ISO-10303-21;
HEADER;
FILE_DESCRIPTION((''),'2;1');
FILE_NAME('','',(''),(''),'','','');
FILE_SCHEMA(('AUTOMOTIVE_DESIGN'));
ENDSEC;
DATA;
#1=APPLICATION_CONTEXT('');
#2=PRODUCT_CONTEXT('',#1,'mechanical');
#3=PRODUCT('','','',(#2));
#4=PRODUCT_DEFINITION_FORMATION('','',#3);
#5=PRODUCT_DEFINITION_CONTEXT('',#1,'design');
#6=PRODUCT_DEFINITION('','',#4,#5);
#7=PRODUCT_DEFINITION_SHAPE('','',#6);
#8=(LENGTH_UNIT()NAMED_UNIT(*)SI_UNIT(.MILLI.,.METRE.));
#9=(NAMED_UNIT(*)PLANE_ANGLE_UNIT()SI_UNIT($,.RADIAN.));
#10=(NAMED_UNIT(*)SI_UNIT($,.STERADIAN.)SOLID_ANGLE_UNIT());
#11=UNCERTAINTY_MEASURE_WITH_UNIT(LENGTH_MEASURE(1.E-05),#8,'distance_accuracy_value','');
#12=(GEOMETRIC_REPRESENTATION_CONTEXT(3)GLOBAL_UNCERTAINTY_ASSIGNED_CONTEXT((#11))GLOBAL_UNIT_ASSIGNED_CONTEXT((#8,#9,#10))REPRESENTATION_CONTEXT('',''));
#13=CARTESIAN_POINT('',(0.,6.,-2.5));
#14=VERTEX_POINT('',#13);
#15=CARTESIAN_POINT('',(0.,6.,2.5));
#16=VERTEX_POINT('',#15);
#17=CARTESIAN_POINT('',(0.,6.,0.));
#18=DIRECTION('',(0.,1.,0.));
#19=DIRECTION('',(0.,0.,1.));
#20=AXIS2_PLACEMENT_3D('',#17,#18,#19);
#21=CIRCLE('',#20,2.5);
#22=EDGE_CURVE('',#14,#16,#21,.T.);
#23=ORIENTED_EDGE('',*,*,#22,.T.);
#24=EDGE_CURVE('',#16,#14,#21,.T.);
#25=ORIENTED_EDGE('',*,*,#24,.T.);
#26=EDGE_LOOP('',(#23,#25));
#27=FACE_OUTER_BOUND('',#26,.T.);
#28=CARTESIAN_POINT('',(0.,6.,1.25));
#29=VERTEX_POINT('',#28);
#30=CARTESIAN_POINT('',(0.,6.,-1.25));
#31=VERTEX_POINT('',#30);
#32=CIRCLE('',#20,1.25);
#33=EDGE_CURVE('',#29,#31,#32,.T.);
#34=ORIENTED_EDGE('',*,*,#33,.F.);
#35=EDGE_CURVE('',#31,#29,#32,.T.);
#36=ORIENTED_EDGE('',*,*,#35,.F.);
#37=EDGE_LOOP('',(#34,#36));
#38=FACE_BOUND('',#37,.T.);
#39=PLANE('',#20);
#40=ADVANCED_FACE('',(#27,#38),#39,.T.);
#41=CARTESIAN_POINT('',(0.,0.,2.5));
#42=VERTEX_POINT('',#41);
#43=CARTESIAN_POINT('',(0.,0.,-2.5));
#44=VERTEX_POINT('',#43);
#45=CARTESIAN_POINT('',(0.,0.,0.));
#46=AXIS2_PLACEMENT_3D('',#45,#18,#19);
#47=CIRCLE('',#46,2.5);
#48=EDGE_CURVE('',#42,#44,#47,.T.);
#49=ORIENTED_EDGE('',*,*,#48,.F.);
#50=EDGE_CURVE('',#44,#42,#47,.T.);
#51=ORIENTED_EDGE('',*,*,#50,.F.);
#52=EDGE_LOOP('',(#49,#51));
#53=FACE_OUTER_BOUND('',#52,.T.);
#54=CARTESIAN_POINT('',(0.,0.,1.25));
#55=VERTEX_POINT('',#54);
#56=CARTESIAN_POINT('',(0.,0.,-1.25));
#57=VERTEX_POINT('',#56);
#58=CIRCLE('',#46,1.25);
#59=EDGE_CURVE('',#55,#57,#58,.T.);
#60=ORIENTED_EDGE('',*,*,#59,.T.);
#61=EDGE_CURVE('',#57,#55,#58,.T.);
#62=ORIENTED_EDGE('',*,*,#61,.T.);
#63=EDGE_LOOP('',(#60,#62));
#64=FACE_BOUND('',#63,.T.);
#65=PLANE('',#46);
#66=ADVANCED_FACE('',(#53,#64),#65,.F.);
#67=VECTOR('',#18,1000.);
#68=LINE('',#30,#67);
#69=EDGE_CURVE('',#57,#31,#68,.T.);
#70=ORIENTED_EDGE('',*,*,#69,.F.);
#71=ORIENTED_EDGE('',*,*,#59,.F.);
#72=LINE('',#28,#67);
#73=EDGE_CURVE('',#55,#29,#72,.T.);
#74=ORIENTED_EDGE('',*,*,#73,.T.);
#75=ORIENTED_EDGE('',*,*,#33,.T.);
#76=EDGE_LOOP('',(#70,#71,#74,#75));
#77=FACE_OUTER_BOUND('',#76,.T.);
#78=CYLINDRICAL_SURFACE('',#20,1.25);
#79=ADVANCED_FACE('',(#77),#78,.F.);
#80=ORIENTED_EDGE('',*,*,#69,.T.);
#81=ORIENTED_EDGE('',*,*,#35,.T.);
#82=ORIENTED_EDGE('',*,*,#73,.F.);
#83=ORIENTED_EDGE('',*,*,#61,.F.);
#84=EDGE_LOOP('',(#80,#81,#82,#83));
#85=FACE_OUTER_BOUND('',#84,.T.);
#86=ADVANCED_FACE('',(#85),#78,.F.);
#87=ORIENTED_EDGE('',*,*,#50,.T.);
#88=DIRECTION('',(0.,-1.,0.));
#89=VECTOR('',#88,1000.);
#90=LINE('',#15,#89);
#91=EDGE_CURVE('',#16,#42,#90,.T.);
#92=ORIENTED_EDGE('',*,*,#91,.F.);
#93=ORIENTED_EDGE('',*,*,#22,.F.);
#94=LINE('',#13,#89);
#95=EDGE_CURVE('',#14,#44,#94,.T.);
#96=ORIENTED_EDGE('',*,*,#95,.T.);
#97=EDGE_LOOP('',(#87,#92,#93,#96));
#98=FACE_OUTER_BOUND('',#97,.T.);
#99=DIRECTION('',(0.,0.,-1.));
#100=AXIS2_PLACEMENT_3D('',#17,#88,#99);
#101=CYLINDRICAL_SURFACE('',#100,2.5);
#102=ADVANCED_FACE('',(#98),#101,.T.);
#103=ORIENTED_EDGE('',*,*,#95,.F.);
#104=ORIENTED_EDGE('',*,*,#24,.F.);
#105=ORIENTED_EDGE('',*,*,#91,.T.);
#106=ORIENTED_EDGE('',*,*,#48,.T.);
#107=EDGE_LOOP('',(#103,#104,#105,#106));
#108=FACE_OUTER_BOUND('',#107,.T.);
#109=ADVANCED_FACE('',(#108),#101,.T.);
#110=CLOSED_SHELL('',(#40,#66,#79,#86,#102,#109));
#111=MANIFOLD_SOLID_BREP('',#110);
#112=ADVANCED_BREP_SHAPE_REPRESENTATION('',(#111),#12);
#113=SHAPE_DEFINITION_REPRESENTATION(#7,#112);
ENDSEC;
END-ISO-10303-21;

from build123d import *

# Parameters (mm, degrees)
SKETCH_1_R         = 2.5
EXTRUDE_1_DEPTH    = 6
HOLE_WIZARD_M3_1_D = 2.5


with BuildPart() as part:
    # 草图1 → 凸台-拉伸1 (new body)
    with BuildSketch(Plane(origin=(0, 0, 0), x_dir=(1, 0, 0), z_dir=(0, 1, 0))):
        with Locations(Location((0, 0, 0), (0, 0, 270))):
            Circle(SKETCH_1_R)
    extrude(amount=EXTRUDE_1_DEPTH)

    # M3 螺纹孔1 (through all)
    with Locations(Plane(origin=(0, 6, 0), x_dir=(1, 0, 0), z_dir=(0, 1, 0))):
        with Locations((0, 0)):
            Hole(HOLE_WIZARD_M3_1_D / 2)


solid = part.part
